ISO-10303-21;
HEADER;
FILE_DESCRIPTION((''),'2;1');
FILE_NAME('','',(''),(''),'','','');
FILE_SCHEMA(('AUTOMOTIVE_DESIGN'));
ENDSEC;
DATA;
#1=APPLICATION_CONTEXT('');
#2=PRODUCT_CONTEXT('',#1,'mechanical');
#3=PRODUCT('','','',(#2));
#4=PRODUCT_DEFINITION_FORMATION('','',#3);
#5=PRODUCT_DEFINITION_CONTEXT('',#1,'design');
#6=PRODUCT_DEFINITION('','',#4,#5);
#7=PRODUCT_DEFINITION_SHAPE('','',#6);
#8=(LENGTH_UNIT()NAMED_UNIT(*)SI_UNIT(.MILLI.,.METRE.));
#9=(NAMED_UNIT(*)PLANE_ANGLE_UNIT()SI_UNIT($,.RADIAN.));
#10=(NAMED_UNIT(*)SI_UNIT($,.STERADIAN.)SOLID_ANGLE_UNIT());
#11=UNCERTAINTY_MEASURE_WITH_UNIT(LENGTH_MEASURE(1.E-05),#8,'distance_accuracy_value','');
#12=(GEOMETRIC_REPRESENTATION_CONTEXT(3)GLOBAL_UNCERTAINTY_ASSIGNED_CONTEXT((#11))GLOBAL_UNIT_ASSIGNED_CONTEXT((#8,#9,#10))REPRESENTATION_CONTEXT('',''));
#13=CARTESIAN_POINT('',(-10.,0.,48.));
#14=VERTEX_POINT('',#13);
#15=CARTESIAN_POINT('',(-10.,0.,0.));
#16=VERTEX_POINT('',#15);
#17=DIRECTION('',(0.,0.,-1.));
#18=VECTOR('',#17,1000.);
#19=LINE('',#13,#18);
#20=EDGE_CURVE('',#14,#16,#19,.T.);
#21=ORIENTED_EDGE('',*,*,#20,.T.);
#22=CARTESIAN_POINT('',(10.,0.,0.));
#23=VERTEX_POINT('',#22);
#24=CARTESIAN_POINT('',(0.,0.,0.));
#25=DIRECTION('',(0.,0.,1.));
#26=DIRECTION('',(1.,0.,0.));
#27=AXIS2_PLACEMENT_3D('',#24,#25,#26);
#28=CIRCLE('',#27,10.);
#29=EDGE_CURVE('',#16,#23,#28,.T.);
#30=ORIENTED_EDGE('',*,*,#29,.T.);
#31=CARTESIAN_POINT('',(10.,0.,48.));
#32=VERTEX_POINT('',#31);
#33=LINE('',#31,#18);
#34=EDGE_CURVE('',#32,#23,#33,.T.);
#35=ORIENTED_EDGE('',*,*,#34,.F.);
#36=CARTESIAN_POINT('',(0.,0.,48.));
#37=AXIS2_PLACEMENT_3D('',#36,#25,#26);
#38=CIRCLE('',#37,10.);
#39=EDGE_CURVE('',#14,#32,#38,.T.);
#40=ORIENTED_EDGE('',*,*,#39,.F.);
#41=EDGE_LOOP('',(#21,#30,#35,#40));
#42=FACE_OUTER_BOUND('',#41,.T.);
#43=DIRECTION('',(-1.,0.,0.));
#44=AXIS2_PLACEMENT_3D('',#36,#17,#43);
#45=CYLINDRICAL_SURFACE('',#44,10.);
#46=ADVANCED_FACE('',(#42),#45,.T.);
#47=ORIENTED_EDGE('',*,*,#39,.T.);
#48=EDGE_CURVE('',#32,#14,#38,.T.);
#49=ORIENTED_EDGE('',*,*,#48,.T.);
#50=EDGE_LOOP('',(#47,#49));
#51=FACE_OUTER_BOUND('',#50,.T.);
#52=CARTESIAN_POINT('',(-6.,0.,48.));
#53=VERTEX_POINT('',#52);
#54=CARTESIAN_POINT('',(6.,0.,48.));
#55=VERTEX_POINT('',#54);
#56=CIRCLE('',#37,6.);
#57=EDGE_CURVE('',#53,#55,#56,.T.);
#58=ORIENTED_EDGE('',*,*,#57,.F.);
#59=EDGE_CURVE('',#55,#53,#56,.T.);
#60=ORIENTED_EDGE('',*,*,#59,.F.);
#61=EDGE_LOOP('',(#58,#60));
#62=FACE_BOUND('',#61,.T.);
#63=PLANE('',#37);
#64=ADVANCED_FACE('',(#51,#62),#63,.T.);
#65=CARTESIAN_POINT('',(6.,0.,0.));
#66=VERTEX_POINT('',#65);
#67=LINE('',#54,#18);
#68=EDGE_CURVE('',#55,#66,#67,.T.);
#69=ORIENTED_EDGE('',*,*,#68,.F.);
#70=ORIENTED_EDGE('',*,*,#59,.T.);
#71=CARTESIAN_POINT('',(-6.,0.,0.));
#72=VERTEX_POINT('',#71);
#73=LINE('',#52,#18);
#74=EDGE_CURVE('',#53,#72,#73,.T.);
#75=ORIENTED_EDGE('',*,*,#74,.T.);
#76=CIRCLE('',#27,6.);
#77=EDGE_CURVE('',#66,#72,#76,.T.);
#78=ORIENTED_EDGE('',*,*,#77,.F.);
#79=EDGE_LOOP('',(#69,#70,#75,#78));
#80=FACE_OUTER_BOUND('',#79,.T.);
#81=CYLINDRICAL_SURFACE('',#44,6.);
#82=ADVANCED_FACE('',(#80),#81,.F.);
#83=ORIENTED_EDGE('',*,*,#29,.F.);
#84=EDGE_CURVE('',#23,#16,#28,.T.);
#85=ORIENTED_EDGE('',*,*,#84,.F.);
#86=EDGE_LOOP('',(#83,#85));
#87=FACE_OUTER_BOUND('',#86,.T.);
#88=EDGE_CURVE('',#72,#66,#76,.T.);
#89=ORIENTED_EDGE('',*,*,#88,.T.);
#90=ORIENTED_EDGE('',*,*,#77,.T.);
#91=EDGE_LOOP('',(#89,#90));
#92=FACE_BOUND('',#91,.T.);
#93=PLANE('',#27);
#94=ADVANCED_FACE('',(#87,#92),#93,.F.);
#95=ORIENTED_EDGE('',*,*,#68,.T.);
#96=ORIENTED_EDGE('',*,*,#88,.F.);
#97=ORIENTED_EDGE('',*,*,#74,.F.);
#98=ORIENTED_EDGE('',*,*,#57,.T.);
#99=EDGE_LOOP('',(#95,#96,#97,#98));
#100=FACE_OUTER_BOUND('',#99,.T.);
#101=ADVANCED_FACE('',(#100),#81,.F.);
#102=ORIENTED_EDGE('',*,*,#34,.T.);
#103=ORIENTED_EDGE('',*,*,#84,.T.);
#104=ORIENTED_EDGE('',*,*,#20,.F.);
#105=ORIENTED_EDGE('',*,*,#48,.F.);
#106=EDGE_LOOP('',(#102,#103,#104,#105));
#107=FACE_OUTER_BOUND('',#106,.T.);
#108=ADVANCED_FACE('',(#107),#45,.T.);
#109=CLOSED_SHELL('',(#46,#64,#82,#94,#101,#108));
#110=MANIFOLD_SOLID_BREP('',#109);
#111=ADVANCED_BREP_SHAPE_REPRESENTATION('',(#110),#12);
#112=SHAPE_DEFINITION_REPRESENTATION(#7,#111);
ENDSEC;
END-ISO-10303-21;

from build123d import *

# Parameters (mm, degrees)
SKETCH1_R           = 10
SKETCH1_R_2         = 6
BOSS_EXTRUDE1_DEPTH = 48


with BuildPart() as part:
    # Sketch1 → Boss-Extrude1 (new body)
    with BuildSketch(Plane.XY):
        Circle(SKETCH1_R)
        Circle(SKETCH1_R_2, mode=Mode.SUBTRACT)
    extrude(amount=BOSS_EXTRUDE1_DEPTH)


solid = part.part
